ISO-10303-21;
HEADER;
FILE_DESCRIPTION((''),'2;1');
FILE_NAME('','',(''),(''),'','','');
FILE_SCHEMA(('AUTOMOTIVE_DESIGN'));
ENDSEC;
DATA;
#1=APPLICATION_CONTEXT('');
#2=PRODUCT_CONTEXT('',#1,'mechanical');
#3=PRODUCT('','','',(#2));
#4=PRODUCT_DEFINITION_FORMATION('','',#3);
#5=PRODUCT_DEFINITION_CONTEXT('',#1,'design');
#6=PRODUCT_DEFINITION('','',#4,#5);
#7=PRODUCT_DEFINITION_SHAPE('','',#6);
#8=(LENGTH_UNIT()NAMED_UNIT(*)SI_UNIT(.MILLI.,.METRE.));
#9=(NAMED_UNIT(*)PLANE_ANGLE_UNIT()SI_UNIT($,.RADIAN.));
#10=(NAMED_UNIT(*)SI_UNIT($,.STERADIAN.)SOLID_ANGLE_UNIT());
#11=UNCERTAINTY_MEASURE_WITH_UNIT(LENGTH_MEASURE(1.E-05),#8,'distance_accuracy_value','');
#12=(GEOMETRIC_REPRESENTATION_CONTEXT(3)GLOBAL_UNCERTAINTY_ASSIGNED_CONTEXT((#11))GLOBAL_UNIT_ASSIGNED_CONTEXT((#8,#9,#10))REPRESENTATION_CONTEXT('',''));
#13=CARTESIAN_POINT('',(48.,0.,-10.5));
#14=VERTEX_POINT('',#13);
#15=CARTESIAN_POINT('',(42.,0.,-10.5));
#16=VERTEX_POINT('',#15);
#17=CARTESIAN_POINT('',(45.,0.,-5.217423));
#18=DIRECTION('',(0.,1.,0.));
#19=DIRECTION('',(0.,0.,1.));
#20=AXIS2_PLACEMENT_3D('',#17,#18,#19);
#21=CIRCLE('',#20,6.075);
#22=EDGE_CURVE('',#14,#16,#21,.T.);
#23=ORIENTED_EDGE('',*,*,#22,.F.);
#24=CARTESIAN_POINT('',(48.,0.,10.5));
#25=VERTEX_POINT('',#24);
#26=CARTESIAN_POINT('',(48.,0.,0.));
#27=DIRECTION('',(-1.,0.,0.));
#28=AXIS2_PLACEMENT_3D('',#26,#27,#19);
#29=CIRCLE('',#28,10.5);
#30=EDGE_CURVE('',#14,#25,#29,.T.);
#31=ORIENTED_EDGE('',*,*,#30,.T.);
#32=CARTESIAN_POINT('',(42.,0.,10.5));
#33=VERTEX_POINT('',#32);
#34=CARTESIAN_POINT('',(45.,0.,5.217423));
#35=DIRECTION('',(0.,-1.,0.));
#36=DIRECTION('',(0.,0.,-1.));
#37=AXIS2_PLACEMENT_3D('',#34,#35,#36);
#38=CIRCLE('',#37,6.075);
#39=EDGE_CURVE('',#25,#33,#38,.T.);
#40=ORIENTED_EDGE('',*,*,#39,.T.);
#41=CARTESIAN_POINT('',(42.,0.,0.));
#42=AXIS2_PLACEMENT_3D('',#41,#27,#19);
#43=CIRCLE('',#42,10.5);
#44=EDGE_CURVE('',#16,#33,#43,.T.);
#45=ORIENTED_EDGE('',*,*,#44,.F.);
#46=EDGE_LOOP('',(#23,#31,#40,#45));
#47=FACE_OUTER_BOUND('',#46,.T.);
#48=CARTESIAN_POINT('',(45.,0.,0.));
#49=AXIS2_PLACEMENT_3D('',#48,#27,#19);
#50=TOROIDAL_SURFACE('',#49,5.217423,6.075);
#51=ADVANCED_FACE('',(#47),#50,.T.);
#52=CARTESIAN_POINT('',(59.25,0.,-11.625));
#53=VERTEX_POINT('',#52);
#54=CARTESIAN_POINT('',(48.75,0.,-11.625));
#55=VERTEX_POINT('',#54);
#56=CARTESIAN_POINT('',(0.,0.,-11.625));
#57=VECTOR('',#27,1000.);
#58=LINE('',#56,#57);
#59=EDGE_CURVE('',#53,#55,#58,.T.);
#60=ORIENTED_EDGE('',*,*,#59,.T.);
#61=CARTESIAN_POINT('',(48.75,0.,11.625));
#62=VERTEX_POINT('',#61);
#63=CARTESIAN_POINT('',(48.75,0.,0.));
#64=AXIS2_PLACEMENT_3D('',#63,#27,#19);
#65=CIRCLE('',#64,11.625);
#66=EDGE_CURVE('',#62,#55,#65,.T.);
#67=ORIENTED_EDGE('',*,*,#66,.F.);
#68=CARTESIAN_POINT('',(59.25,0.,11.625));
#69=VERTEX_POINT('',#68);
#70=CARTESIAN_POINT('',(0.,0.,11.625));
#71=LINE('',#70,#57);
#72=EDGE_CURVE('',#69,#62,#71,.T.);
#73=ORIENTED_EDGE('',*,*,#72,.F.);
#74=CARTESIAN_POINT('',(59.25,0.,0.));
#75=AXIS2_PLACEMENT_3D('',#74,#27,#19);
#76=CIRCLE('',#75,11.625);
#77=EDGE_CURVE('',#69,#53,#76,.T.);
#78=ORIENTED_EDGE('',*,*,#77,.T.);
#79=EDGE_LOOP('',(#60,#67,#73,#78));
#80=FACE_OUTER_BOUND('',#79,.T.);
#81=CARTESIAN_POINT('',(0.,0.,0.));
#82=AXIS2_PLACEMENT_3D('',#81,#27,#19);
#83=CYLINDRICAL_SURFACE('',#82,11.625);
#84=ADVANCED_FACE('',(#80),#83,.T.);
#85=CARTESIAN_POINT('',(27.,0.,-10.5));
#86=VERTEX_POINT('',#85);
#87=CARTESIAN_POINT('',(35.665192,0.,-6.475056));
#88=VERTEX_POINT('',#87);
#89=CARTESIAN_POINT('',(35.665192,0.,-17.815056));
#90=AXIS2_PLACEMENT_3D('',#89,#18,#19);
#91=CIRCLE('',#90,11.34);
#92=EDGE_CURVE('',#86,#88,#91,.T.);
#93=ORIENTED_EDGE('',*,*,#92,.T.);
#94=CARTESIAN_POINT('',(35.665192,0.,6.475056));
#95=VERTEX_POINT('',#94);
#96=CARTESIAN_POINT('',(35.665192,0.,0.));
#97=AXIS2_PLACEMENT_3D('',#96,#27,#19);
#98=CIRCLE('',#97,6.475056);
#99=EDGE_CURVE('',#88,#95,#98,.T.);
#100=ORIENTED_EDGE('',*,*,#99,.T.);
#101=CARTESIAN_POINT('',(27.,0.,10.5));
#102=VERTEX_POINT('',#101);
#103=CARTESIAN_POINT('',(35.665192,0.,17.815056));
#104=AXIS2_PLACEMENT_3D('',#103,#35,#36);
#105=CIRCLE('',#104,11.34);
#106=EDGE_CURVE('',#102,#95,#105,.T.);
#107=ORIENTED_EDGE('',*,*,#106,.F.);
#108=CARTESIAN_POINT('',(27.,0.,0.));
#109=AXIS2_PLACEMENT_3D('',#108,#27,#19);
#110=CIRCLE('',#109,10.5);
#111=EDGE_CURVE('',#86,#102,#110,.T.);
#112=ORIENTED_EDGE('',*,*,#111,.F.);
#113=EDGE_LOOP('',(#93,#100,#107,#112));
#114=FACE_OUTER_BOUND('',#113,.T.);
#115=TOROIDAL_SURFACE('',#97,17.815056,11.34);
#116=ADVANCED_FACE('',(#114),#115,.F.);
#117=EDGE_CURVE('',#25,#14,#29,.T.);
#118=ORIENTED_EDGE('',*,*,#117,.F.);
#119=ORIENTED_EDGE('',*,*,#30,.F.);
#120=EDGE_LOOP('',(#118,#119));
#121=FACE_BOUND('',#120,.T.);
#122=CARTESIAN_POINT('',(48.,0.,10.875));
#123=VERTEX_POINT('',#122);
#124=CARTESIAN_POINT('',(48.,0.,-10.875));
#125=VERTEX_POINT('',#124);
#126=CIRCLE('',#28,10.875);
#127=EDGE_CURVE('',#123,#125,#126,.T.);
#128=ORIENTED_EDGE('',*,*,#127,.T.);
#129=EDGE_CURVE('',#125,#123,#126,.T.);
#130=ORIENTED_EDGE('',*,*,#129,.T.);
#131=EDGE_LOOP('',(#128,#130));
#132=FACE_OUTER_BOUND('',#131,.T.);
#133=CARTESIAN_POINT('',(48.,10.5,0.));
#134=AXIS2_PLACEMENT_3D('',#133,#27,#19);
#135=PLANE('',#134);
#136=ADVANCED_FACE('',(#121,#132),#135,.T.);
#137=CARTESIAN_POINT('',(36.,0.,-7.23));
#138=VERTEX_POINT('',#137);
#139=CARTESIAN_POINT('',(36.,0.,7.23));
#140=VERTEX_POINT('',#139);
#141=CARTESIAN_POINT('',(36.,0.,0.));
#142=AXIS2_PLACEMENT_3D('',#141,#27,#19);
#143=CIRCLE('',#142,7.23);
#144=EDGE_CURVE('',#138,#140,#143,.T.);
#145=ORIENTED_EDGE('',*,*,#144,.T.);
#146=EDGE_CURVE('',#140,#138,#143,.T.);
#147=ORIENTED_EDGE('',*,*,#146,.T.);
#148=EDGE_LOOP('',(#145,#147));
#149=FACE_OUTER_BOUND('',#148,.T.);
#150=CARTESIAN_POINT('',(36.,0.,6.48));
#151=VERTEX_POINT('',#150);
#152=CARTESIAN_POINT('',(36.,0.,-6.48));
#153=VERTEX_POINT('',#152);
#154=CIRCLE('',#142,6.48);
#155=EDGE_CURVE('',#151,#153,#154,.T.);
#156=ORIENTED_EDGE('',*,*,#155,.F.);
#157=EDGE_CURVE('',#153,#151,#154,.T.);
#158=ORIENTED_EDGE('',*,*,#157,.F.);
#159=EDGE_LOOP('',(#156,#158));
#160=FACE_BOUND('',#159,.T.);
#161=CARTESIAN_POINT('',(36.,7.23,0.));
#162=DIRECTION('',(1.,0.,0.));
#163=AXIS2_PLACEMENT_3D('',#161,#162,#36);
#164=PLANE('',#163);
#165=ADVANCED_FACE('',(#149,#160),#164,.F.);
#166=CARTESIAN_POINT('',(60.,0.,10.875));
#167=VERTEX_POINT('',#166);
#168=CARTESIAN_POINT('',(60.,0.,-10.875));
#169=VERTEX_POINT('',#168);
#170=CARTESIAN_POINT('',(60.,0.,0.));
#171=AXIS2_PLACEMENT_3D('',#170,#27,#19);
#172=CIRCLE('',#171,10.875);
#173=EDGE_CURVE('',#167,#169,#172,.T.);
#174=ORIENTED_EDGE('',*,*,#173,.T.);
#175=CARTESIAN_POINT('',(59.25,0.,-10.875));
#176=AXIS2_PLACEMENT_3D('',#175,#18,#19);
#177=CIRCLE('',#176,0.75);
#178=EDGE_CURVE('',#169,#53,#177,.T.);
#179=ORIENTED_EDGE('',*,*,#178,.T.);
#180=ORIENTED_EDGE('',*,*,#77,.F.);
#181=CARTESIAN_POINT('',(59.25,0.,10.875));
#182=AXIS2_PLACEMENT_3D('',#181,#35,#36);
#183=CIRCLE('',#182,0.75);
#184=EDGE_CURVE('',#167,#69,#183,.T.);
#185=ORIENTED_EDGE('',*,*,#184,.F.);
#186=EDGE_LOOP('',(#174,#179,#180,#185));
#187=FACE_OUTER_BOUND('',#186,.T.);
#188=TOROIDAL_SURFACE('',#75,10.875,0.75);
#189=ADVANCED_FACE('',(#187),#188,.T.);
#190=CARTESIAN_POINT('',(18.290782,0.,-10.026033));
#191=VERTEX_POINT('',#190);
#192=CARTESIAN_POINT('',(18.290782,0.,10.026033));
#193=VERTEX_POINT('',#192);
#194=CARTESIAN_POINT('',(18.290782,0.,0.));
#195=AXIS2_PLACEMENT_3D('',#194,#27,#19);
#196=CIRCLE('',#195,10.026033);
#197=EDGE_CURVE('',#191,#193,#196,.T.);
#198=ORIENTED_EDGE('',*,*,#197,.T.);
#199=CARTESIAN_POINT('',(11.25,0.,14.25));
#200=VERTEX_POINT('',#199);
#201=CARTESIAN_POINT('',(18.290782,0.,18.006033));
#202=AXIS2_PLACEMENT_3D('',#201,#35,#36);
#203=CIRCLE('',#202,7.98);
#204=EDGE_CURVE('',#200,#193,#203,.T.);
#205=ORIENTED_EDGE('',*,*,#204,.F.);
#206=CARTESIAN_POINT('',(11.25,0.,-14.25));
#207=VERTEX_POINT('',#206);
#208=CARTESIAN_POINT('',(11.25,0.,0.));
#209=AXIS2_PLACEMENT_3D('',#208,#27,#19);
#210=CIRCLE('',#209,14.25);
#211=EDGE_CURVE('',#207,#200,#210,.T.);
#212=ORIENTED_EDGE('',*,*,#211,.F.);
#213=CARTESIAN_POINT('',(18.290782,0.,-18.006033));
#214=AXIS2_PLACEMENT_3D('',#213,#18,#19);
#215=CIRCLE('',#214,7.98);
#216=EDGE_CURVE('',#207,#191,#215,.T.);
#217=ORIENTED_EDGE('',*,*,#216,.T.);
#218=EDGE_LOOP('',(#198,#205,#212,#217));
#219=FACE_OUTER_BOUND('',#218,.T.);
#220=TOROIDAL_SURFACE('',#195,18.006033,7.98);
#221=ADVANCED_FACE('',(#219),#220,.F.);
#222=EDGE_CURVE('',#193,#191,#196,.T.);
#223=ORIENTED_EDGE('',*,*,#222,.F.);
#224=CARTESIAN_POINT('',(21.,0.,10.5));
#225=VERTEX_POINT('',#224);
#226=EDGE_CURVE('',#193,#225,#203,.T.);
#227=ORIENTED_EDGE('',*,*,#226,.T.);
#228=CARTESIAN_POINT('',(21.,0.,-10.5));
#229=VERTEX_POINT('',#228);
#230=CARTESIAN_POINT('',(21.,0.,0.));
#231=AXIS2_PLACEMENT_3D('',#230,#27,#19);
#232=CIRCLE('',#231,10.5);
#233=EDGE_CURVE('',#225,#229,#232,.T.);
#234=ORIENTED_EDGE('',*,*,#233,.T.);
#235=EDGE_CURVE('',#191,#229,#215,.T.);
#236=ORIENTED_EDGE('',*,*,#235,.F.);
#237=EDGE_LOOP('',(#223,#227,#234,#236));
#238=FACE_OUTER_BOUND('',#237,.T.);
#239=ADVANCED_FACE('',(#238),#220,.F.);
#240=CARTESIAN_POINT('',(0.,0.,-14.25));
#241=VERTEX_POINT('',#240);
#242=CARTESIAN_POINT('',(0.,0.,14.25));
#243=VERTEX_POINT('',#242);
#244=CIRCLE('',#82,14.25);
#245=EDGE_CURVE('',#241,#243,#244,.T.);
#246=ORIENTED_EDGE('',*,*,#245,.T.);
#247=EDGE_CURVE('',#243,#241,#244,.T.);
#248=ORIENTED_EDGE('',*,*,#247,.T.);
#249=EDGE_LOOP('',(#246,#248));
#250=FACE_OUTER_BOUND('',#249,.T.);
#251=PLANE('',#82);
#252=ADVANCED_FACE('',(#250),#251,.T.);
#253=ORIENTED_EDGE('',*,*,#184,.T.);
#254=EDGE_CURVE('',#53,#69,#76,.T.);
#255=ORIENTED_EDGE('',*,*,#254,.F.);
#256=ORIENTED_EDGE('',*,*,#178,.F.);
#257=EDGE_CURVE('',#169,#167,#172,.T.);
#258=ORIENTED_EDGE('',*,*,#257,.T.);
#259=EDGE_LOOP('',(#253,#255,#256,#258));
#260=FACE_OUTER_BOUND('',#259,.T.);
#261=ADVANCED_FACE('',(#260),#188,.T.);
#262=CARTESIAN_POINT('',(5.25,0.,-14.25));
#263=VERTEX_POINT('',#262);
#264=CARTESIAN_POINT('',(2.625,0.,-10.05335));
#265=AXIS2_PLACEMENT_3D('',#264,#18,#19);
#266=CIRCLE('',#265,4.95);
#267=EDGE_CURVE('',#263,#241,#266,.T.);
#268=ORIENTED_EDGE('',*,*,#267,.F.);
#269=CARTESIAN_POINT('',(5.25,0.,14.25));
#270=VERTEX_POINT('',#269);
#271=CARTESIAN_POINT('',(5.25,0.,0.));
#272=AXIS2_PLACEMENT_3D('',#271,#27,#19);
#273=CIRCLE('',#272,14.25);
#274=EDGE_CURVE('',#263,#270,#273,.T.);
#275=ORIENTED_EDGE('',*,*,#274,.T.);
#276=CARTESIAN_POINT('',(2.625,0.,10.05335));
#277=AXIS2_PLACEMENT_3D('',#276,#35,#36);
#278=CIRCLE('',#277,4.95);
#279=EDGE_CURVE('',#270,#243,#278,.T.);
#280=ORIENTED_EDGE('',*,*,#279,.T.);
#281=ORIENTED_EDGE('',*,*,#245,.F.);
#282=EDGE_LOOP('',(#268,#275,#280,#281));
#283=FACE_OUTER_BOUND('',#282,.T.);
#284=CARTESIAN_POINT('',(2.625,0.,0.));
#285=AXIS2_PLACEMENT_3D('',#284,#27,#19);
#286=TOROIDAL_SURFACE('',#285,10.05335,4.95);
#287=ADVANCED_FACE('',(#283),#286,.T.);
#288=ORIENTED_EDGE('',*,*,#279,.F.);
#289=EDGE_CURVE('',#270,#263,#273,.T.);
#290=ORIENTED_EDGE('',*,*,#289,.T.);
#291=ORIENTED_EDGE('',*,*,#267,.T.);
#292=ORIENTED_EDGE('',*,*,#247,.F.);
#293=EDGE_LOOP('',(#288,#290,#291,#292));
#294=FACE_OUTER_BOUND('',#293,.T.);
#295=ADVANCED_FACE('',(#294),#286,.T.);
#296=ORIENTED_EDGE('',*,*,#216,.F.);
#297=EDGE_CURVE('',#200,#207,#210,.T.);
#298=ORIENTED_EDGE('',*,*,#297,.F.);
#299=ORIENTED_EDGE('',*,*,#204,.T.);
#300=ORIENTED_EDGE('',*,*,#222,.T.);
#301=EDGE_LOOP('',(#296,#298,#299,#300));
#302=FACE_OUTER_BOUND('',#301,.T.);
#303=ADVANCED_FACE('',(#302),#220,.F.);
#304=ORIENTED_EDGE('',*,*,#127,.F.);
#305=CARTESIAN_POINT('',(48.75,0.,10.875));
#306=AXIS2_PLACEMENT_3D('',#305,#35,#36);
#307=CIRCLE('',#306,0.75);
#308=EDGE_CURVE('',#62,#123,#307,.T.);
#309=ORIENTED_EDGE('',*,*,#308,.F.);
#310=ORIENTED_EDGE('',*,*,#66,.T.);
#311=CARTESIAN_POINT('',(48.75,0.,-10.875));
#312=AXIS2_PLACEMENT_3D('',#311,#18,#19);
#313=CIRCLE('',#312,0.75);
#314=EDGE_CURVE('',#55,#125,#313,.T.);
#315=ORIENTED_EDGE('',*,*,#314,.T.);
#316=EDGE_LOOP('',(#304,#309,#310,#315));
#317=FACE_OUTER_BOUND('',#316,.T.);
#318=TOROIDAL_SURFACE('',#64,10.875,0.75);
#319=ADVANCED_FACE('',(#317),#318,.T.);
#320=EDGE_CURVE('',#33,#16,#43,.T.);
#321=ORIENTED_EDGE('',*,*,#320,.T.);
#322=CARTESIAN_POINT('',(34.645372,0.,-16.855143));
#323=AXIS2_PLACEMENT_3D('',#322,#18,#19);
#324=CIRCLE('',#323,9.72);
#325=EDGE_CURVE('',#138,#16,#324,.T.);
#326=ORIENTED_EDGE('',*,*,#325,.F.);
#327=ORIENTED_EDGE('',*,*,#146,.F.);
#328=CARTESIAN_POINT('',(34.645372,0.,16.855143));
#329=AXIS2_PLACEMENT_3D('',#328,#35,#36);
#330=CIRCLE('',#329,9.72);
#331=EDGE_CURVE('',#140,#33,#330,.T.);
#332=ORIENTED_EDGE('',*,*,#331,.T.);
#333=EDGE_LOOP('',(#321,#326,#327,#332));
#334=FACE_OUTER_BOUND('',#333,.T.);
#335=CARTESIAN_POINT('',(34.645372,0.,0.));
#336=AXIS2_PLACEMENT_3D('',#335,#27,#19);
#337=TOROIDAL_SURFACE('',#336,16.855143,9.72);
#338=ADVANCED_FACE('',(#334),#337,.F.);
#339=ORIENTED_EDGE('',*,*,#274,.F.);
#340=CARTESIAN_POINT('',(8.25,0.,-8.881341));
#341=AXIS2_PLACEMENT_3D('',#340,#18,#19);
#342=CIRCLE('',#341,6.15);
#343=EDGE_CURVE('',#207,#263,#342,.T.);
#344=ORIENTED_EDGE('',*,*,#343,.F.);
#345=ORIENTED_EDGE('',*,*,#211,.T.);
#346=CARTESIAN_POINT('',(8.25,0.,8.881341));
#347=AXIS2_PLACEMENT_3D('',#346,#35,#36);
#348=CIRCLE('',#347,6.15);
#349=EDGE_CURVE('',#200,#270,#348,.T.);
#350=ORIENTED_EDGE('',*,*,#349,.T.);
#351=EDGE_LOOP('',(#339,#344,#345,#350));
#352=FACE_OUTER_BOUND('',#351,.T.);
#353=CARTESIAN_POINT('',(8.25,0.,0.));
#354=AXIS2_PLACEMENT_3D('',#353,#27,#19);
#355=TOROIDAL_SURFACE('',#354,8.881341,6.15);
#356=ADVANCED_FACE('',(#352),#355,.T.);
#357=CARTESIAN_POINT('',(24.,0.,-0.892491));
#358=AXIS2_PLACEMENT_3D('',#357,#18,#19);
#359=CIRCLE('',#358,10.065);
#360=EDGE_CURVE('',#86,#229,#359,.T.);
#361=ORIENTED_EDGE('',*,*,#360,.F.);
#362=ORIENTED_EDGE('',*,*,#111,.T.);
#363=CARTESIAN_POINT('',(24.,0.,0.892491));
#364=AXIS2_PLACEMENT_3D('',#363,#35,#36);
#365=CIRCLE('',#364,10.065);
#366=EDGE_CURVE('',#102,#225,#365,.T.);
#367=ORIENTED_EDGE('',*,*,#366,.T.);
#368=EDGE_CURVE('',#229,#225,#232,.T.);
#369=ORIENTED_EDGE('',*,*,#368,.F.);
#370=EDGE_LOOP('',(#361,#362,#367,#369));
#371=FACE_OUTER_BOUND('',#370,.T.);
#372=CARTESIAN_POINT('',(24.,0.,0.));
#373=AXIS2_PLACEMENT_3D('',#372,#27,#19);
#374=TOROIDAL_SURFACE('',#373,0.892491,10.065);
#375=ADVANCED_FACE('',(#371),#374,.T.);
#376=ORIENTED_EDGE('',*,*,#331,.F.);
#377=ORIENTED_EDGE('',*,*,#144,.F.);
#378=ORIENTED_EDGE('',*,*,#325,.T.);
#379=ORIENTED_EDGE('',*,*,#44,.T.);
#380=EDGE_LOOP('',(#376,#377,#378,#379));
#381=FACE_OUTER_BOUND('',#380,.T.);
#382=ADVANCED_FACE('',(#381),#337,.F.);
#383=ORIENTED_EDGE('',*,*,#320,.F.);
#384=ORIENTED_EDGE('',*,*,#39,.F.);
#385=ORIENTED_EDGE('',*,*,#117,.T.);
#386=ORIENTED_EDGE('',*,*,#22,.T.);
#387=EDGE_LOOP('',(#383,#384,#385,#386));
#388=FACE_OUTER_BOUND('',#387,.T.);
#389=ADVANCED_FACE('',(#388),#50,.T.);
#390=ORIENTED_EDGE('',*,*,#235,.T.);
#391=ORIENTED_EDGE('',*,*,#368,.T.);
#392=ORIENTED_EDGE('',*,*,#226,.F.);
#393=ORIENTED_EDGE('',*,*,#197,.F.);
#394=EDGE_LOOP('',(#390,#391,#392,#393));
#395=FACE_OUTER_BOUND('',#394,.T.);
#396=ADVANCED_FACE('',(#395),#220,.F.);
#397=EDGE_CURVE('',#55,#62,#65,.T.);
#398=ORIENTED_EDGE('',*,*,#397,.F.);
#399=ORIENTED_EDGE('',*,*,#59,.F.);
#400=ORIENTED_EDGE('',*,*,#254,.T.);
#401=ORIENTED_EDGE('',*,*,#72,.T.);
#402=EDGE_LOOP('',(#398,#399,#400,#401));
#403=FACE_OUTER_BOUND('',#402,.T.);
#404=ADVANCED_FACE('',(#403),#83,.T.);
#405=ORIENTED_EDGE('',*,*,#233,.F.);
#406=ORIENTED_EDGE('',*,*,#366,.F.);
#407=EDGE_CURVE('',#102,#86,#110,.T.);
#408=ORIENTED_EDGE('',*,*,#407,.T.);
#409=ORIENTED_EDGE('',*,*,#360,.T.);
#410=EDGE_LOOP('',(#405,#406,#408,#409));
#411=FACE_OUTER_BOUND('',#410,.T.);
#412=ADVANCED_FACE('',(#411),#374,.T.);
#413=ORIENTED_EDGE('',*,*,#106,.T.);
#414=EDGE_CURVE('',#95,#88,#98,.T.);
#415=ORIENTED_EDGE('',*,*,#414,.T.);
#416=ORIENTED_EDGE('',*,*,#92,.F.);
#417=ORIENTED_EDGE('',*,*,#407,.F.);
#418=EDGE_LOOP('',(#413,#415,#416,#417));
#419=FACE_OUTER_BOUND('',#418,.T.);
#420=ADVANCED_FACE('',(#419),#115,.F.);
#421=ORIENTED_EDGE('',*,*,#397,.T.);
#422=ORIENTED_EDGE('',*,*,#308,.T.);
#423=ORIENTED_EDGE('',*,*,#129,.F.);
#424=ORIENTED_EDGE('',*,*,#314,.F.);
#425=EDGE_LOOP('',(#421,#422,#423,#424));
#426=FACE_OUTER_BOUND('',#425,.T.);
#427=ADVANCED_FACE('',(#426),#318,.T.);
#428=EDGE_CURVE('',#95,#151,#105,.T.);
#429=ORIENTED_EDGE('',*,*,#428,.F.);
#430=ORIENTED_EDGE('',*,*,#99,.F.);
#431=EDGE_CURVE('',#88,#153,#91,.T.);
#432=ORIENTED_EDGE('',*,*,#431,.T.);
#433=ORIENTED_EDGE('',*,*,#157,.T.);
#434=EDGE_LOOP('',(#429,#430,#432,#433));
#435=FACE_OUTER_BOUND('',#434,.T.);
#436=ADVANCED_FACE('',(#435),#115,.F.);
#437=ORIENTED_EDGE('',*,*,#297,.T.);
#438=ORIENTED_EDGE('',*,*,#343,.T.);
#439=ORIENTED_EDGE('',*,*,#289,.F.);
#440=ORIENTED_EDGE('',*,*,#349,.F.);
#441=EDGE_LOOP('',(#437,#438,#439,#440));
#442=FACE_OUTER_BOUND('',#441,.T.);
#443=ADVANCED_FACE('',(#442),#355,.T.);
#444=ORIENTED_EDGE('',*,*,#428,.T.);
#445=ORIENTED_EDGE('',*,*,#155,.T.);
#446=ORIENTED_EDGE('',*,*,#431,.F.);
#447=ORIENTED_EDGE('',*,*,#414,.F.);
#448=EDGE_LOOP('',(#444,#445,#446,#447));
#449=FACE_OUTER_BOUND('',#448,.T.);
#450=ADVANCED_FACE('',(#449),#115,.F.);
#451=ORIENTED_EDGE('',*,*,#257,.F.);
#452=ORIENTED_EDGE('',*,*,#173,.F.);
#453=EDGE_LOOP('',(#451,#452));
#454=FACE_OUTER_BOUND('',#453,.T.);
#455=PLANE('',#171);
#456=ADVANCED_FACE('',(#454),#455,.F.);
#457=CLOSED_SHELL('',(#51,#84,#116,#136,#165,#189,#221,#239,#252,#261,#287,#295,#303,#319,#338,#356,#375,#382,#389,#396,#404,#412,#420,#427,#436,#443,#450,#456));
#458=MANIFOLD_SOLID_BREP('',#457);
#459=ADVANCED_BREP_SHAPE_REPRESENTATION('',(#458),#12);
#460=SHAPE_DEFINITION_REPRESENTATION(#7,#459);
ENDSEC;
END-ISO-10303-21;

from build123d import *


with BuildPart() as part:
    # Shaft Half-Profile Sketch → Shaft Body Revolve 360° (revolve)
    with BuildSketch(Plane.XY, mode=Mode.PRIVATE) as shaft_body_revolve_360_sk:
        with BuildLine():
            Line((0, 0), (60, 0))
            Line((60, 0), (60, -10.875))
            ThreePointArc((60, -10.875), (59.780330086, -11.405330086), (59.25, -11.625))
            Line((59.25, -11.625), (48.75, -11.625))
            ThreePointArc((48.75, -11.625), (48.219669914, -11.405330086), (48, -10.875))
            Line((48, -10.875), (48, -10.5))
            ThreePointArc((48, -10.5), (45, -11.292422504), (42, -10.5))
            ThreePointArc((42, -10.5), (39.296824458, -8.320367966), (36, -7.23))
            Line((36, -7.23), (36, -6.48))
            ThreePointArc((36, -6.48), (31.040375838, -7.460990683), (27, -10.5))
            ThreePointArc((27, -10.5), (24, -10.957491218), (21, -10.5))
            ThreePointArc((21, -10.5), (15.426129049, -10.557935528), (11.25, -14.25))
            ThreePointArc((11.25, -14.25), (8.25, -15.03134095), (5.25, -14.25))
            ThreePointArc((5.25, -14.25), (2.625, -15.00334955), (0, -14.25))
            Line((0, -14.25), (0, 0))
        make_face()
    revolve(shaft_body_revolve_360_sk.sketch.rotate(Axis((0, 0, 0), (1, 0, 0)), 270), axis=Axis((0, 0, 0), (1, 0, 0)))


solid = part.part
